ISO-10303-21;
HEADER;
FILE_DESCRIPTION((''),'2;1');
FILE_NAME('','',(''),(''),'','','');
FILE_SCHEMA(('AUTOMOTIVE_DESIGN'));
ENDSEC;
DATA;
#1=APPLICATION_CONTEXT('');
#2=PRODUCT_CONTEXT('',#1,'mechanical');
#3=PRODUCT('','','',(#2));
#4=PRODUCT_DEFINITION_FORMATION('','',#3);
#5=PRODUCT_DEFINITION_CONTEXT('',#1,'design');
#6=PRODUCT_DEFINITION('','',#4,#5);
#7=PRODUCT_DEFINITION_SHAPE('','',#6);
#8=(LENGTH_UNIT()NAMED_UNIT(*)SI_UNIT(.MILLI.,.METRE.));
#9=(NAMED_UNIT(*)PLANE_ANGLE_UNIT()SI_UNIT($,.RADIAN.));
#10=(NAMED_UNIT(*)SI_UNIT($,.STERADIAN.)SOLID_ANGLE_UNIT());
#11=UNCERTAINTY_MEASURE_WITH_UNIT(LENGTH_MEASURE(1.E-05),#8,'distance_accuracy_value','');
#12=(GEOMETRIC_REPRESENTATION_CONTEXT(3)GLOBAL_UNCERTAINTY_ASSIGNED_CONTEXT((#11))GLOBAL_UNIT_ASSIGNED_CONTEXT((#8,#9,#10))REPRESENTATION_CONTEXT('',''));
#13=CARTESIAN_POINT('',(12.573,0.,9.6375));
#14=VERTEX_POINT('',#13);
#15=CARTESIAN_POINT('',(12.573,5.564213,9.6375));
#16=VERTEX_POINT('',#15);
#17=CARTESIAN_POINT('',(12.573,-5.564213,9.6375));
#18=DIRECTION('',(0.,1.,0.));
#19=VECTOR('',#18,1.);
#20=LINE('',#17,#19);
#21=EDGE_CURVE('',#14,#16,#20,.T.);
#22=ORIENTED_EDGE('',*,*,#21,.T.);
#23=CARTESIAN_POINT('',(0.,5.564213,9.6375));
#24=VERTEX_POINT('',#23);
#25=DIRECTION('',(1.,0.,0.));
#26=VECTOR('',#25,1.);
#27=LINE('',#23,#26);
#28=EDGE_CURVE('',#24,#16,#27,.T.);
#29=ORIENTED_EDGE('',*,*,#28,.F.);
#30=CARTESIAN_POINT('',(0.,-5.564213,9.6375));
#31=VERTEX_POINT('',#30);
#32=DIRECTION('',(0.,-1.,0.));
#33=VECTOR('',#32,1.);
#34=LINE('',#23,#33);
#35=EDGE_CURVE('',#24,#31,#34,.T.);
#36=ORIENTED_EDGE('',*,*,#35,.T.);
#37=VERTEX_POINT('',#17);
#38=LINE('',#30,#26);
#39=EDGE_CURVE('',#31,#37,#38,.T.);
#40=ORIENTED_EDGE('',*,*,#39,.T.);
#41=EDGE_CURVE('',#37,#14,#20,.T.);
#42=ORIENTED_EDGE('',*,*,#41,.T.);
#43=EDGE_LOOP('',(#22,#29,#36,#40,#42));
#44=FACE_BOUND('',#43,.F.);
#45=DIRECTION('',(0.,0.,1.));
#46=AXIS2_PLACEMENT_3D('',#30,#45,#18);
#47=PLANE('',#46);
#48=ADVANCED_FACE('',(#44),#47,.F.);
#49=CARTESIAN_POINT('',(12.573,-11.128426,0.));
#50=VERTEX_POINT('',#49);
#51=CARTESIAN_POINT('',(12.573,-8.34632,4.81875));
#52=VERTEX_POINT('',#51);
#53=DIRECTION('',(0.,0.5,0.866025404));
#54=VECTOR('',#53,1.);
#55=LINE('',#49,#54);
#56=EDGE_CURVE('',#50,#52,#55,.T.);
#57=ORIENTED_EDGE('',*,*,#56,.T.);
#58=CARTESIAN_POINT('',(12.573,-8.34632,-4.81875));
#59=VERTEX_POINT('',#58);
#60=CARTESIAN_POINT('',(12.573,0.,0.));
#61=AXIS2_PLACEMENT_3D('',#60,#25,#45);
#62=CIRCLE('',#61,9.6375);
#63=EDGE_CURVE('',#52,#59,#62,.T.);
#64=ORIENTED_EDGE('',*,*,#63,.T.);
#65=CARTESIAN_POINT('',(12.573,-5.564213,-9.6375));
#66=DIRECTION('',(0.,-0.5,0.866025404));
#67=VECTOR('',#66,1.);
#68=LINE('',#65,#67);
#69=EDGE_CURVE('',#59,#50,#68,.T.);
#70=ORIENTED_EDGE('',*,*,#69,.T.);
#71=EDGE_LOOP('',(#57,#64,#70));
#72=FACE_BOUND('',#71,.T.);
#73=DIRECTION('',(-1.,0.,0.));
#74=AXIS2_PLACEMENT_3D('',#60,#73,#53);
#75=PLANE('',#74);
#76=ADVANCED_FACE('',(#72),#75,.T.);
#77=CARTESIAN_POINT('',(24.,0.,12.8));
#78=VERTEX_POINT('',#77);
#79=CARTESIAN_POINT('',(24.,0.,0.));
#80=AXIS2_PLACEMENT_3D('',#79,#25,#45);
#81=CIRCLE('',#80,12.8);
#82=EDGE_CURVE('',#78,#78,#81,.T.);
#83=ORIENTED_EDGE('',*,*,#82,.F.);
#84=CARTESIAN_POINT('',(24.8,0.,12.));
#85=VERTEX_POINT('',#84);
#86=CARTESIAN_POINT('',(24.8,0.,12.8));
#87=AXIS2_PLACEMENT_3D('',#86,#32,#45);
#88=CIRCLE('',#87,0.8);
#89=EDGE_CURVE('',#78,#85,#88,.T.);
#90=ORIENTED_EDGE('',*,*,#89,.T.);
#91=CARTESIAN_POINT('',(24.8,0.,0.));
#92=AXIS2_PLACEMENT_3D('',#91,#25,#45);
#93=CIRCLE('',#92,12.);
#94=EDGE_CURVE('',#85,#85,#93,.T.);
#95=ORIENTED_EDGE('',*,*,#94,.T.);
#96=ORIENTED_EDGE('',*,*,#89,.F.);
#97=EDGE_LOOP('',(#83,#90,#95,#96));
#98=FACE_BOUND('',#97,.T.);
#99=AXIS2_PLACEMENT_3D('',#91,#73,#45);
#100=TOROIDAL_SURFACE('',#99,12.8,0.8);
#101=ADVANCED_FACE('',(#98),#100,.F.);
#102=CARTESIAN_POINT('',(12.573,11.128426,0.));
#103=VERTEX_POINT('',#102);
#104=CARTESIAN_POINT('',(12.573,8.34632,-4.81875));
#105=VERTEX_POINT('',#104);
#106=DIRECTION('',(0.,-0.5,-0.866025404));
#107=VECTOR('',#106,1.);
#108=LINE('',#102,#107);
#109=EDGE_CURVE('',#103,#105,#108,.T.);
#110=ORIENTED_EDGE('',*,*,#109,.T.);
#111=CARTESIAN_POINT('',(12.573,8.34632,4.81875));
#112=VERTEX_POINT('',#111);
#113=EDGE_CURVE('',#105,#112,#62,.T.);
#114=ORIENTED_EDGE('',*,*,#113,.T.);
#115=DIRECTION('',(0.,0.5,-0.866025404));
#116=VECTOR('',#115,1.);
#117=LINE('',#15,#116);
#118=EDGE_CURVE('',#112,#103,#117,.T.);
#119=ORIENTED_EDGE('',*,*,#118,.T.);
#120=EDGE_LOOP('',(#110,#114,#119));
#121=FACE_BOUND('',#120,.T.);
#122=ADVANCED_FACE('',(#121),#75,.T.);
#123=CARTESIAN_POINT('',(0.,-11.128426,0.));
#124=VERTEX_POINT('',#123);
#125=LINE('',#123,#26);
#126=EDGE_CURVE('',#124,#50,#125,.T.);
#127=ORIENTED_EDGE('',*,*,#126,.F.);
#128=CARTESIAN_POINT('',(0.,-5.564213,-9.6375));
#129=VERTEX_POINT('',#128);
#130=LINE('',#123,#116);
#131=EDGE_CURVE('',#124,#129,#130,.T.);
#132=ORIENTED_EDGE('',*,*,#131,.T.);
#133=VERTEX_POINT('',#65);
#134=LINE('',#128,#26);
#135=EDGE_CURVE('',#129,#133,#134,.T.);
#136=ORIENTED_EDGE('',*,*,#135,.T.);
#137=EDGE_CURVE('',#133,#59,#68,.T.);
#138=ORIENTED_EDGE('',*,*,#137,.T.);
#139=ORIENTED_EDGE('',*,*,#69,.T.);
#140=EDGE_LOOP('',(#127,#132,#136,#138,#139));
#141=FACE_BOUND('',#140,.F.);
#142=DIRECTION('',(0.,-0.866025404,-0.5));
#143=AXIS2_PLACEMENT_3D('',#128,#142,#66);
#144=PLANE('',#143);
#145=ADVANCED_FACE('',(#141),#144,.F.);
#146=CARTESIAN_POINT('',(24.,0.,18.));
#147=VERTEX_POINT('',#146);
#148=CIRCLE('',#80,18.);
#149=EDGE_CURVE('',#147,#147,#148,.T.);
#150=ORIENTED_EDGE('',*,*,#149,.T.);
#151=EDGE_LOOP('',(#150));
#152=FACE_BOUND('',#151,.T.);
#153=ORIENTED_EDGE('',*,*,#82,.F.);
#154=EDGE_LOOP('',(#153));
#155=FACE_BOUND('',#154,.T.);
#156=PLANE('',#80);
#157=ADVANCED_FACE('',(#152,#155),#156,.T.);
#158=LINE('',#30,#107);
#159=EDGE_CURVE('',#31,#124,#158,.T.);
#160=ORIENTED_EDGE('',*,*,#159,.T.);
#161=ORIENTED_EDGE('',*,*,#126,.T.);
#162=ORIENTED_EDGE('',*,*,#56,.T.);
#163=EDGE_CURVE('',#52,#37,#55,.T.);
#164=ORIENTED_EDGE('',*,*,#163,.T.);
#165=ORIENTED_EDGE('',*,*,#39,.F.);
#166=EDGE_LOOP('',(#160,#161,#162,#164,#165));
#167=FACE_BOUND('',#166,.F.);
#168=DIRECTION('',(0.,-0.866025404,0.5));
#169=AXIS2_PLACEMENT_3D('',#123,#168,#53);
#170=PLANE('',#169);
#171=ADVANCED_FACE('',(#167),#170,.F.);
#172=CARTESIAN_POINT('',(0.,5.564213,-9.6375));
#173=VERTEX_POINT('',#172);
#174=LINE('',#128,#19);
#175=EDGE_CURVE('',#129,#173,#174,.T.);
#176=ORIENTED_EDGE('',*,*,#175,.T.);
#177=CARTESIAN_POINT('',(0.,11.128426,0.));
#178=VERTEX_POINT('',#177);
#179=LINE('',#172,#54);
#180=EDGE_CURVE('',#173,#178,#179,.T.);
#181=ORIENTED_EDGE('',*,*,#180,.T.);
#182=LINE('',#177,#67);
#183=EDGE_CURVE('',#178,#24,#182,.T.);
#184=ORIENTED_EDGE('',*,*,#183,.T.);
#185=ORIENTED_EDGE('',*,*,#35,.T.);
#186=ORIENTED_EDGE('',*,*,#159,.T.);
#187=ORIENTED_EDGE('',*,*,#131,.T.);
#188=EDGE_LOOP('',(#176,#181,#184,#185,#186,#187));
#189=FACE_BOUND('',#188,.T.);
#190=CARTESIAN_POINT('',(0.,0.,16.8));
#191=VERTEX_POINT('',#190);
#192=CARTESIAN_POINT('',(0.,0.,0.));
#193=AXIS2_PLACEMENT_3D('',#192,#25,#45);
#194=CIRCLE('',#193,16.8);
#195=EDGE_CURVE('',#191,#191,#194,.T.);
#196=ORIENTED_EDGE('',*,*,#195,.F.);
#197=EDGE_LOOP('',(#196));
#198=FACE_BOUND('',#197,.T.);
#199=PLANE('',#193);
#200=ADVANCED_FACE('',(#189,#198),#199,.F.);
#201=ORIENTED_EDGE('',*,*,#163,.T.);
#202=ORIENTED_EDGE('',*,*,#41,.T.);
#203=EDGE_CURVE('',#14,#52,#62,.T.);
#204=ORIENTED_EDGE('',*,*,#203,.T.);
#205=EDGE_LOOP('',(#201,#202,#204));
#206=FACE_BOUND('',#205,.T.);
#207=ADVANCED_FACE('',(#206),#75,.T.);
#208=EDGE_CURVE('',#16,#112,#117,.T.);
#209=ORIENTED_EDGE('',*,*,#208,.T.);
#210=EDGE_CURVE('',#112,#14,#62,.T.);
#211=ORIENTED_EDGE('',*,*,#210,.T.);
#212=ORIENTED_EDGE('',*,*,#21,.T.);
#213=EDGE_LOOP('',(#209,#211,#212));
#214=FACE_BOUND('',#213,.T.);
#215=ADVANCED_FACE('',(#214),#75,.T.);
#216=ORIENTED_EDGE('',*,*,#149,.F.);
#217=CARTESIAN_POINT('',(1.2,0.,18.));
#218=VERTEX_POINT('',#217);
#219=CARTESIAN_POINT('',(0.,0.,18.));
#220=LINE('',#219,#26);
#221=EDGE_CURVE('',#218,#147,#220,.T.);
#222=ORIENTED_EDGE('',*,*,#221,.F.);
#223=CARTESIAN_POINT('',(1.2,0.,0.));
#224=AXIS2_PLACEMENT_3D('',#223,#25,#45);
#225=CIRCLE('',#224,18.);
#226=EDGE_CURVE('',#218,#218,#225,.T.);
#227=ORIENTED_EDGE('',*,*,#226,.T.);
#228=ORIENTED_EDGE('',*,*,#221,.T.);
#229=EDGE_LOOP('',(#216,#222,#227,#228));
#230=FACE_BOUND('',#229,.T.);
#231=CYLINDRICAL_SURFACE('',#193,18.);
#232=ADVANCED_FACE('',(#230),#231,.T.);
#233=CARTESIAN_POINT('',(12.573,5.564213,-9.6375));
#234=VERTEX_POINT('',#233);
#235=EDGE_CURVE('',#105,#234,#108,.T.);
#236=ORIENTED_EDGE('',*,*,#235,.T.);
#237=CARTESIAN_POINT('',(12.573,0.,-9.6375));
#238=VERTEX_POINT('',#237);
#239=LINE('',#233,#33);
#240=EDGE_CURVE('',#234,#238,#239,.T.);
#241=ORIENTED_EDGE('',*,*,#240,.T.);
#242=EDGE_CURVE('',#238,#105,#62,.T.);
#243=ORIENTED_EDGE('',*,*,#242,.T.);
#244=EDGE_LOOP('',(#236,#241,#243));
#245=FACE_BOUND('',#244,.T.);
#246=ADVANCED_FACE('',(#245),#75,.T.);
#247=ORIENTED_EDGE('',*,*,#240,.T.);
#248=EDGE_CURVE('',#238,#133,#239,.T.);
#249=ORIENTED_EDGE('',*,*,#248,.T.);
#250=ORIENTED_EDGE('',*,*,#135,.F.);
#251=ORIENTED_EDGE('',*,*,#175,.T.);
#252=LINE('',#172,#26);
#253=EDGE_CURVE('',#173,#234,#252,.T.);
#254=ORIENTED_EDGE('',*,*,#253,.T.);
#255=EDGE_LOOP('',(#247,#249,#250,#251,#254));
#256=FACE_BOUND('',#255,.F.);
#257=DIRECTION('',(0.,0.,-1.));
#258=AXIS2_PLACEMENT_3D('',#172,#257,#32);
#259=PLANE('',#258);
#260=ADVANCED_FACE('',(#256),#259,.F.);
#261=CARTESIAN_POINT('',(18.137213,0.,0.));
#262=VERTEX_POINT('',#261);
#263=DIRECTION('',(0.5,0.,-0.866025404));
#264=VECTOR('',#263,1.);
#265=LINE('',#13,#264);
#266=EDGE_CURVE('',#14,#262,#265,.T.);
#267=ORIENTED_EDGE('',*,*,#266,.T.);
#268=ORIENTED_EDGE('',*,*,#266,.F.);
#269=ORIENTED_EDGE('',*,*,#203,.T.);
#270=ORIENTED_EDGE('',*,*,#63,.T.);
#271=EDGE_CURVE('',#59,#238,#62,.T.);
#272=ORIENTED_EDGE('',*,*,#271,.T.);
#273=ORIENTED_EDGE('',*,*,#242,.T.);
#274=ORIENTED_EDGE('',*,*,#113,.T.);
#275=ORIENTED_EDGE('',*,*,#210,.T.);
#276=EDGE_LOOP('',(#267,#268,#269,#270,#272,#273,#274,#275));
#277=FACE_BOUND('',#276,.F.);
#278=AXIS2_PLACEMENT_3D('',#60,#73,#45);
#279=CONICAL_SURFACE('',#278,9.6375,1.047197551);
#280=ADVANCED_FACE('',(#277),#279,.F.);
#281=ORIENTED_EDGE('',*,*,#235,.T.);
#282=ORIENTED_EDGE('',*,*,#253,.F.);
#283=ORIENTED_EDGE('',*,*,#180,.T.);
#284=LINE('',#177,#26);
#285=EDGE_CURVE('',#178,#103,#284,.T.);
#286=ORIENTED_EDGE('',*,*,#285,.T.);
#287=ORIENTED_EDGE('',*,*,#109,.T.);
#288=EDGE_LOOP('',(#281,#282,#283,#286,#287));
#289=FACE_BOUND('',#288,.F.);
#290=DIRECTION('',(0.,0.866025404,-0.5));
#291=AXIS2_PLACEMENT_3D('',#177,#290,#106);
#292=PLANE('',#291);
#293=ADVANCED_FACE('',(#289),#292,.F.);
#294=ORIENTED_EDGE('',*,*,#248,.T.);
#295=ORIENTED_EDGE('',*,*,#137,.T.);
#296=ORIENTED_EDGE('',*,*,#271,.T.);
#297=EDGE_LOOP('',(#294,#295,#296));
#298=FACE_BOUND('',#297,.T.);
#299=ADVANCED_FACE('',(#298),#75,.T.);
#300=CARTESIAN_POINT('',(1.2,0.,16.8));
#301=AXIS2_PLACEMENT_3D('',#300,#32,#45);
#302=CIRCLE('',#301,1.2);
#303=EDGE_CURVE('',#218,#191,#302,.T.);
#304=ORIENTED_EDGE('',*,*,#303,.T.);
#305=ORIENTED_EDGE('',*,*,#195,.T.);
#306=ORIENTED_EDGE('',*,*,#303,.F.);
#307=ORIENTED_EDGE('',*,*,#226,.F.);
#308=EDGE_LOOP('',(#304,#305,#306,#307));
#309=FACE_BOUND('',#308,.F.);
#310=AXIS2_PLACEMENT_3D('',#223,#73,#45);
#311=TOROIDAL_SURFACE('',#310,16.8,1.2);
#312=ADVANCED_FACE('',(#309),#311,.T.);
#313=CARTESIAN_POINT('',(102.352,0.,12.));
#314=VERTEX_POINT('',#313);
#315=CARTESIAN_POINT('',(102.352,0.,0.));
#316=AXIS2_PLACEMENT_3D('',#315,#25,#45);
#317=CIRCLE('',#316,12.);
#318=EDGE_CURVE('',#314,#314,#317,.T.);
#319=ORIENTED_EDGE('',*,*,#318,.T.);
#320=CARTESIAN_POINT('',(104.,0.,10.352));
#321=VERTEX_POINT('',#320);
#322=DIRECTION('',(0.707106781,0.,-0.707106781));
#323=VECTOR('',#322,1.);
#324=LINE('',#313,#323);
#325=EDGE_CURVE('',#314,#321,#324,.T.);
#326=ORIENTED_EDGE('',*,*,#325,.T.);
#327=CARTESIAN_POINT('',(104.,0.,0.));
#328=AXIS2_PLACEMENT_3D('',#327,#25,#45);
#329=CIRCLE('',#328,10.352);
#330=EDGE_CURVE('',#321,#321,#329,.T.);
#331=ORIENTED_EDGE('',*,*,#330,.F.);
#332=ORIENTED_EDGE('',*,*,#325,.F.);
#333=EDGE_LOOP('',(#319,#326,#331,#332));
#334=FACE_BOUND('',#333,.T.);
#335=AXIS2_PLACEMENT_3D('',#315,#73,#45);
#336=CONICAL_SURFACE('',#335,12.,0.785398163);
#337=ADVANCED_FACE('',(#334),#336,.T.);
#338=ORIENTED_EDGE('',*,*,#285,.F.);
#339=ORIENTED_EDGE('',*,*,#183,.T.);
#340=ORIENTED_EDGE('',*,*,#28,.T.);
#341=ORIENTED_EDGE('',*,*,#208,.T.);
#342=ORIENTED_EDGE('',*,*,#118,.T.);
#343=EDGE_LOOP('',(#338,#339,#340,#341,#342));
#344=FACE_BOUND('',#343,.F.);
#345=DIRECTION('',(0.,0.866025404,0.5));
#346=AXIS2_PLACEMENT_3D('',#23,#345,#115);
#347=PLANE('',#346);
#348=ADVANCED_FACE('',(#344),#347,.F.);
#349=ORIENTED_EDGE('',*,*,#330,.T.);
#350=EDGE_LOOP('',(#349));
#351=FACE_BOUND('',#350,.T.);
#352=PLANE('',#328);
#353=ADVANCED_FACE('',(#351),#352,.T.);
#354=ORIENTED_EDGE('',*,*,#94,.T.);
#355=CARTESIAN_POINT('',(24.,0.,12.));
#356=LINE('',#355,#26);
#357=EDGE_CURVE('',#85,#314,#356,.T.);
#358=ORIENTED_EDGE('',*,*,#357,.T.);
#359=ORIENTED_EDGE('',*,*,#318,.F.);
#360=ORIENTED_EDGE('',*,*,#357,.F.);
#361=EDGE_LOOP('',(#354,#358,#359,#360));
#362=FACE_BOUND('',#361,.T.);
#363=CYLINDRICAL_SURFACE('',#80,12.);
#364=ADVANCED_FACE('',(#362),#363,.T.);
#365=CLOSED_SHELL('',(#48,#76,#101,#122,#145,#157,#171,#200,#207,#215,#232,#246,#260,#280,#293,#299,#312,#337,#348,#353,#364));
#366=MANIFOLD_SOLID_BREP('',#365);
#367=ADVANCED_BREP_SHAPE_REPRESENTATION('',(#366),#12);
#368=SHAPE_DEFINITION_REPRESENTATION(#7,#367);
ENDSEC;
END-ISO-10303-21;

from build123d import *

# Parameters (mm, degrees)
FILLET1_R   = 0.8
FILLET2_R   = 1.2
HEX_2_DEPTH = 12.573


with BuildPart() as part:
    # BodySke → Base-Revolve (revolve)
    with BuildSketch(Plane.XY, mode=Mode.PRIVATE) as base_revolve_sk:
        Polygon((0, 0), (0, 18), (24, 18), (24, 12), (102.352, 12), (104, 10.352), (104, 0), align=None)
    revolve(base_revolve_sk.sketch.rotate(Axis((-31.75, 0, 0), (1, 0, 0)), 90), axis=Axis((-31.75, 0, 0), (1, 0, 0)))

    # Fillet1
    fillet1_edges = [part.edges().sort_by_distance(p)[0] for p in [
        (24, 0, -12),
    ]]
    fillet(fillet1_edges, radius=FILLET1_R)

    # Fillet2
    fillet2_edges = [part.edges().sort_by_distance(p)[0] for p in [
        (0, 0, -18),
    ]]
    fillet(fillet2_edges, radius=FILLET2_R)

    # Sketch2 → Hex-PreBroach (revolve, cut)
    with BuildSketch(Plane.XY, mode=Mode.PRIVATE) as hex_prebroach_sk:
        Polygon((0, 9.6375), (12.573, 9.6375), (18.137213219, 0), (0, 0), align=None)
    revolve(hex_prebroach_sk.sketch.rotate(Axis((0, 0, 0), (1, 0, 0)), 90), axis=Axis((0, 0, 0), (1, 0, 0)), mode=Mode.SUBTRACT)

    # Sketch3 → Hex 2 (cut)
    with BuildSketch(Plane(origin=(0, 0, 0), x_dir=(0, 0.500000000000001, 0.866025403784438), z_dir=(-1, 0, 0))):
        Polygon((5.564213219, 9.6375), (-5.564213219, 9.6375), (-11.128426439, 0), (-5.564213219, -9.6375), (5.564213219, -9.6375), (11.128426439, 0), align=None)
    extrude(amount=-HEX_2_DEPTH, mode=Mode.SUBTRACT)


solid = part.part
